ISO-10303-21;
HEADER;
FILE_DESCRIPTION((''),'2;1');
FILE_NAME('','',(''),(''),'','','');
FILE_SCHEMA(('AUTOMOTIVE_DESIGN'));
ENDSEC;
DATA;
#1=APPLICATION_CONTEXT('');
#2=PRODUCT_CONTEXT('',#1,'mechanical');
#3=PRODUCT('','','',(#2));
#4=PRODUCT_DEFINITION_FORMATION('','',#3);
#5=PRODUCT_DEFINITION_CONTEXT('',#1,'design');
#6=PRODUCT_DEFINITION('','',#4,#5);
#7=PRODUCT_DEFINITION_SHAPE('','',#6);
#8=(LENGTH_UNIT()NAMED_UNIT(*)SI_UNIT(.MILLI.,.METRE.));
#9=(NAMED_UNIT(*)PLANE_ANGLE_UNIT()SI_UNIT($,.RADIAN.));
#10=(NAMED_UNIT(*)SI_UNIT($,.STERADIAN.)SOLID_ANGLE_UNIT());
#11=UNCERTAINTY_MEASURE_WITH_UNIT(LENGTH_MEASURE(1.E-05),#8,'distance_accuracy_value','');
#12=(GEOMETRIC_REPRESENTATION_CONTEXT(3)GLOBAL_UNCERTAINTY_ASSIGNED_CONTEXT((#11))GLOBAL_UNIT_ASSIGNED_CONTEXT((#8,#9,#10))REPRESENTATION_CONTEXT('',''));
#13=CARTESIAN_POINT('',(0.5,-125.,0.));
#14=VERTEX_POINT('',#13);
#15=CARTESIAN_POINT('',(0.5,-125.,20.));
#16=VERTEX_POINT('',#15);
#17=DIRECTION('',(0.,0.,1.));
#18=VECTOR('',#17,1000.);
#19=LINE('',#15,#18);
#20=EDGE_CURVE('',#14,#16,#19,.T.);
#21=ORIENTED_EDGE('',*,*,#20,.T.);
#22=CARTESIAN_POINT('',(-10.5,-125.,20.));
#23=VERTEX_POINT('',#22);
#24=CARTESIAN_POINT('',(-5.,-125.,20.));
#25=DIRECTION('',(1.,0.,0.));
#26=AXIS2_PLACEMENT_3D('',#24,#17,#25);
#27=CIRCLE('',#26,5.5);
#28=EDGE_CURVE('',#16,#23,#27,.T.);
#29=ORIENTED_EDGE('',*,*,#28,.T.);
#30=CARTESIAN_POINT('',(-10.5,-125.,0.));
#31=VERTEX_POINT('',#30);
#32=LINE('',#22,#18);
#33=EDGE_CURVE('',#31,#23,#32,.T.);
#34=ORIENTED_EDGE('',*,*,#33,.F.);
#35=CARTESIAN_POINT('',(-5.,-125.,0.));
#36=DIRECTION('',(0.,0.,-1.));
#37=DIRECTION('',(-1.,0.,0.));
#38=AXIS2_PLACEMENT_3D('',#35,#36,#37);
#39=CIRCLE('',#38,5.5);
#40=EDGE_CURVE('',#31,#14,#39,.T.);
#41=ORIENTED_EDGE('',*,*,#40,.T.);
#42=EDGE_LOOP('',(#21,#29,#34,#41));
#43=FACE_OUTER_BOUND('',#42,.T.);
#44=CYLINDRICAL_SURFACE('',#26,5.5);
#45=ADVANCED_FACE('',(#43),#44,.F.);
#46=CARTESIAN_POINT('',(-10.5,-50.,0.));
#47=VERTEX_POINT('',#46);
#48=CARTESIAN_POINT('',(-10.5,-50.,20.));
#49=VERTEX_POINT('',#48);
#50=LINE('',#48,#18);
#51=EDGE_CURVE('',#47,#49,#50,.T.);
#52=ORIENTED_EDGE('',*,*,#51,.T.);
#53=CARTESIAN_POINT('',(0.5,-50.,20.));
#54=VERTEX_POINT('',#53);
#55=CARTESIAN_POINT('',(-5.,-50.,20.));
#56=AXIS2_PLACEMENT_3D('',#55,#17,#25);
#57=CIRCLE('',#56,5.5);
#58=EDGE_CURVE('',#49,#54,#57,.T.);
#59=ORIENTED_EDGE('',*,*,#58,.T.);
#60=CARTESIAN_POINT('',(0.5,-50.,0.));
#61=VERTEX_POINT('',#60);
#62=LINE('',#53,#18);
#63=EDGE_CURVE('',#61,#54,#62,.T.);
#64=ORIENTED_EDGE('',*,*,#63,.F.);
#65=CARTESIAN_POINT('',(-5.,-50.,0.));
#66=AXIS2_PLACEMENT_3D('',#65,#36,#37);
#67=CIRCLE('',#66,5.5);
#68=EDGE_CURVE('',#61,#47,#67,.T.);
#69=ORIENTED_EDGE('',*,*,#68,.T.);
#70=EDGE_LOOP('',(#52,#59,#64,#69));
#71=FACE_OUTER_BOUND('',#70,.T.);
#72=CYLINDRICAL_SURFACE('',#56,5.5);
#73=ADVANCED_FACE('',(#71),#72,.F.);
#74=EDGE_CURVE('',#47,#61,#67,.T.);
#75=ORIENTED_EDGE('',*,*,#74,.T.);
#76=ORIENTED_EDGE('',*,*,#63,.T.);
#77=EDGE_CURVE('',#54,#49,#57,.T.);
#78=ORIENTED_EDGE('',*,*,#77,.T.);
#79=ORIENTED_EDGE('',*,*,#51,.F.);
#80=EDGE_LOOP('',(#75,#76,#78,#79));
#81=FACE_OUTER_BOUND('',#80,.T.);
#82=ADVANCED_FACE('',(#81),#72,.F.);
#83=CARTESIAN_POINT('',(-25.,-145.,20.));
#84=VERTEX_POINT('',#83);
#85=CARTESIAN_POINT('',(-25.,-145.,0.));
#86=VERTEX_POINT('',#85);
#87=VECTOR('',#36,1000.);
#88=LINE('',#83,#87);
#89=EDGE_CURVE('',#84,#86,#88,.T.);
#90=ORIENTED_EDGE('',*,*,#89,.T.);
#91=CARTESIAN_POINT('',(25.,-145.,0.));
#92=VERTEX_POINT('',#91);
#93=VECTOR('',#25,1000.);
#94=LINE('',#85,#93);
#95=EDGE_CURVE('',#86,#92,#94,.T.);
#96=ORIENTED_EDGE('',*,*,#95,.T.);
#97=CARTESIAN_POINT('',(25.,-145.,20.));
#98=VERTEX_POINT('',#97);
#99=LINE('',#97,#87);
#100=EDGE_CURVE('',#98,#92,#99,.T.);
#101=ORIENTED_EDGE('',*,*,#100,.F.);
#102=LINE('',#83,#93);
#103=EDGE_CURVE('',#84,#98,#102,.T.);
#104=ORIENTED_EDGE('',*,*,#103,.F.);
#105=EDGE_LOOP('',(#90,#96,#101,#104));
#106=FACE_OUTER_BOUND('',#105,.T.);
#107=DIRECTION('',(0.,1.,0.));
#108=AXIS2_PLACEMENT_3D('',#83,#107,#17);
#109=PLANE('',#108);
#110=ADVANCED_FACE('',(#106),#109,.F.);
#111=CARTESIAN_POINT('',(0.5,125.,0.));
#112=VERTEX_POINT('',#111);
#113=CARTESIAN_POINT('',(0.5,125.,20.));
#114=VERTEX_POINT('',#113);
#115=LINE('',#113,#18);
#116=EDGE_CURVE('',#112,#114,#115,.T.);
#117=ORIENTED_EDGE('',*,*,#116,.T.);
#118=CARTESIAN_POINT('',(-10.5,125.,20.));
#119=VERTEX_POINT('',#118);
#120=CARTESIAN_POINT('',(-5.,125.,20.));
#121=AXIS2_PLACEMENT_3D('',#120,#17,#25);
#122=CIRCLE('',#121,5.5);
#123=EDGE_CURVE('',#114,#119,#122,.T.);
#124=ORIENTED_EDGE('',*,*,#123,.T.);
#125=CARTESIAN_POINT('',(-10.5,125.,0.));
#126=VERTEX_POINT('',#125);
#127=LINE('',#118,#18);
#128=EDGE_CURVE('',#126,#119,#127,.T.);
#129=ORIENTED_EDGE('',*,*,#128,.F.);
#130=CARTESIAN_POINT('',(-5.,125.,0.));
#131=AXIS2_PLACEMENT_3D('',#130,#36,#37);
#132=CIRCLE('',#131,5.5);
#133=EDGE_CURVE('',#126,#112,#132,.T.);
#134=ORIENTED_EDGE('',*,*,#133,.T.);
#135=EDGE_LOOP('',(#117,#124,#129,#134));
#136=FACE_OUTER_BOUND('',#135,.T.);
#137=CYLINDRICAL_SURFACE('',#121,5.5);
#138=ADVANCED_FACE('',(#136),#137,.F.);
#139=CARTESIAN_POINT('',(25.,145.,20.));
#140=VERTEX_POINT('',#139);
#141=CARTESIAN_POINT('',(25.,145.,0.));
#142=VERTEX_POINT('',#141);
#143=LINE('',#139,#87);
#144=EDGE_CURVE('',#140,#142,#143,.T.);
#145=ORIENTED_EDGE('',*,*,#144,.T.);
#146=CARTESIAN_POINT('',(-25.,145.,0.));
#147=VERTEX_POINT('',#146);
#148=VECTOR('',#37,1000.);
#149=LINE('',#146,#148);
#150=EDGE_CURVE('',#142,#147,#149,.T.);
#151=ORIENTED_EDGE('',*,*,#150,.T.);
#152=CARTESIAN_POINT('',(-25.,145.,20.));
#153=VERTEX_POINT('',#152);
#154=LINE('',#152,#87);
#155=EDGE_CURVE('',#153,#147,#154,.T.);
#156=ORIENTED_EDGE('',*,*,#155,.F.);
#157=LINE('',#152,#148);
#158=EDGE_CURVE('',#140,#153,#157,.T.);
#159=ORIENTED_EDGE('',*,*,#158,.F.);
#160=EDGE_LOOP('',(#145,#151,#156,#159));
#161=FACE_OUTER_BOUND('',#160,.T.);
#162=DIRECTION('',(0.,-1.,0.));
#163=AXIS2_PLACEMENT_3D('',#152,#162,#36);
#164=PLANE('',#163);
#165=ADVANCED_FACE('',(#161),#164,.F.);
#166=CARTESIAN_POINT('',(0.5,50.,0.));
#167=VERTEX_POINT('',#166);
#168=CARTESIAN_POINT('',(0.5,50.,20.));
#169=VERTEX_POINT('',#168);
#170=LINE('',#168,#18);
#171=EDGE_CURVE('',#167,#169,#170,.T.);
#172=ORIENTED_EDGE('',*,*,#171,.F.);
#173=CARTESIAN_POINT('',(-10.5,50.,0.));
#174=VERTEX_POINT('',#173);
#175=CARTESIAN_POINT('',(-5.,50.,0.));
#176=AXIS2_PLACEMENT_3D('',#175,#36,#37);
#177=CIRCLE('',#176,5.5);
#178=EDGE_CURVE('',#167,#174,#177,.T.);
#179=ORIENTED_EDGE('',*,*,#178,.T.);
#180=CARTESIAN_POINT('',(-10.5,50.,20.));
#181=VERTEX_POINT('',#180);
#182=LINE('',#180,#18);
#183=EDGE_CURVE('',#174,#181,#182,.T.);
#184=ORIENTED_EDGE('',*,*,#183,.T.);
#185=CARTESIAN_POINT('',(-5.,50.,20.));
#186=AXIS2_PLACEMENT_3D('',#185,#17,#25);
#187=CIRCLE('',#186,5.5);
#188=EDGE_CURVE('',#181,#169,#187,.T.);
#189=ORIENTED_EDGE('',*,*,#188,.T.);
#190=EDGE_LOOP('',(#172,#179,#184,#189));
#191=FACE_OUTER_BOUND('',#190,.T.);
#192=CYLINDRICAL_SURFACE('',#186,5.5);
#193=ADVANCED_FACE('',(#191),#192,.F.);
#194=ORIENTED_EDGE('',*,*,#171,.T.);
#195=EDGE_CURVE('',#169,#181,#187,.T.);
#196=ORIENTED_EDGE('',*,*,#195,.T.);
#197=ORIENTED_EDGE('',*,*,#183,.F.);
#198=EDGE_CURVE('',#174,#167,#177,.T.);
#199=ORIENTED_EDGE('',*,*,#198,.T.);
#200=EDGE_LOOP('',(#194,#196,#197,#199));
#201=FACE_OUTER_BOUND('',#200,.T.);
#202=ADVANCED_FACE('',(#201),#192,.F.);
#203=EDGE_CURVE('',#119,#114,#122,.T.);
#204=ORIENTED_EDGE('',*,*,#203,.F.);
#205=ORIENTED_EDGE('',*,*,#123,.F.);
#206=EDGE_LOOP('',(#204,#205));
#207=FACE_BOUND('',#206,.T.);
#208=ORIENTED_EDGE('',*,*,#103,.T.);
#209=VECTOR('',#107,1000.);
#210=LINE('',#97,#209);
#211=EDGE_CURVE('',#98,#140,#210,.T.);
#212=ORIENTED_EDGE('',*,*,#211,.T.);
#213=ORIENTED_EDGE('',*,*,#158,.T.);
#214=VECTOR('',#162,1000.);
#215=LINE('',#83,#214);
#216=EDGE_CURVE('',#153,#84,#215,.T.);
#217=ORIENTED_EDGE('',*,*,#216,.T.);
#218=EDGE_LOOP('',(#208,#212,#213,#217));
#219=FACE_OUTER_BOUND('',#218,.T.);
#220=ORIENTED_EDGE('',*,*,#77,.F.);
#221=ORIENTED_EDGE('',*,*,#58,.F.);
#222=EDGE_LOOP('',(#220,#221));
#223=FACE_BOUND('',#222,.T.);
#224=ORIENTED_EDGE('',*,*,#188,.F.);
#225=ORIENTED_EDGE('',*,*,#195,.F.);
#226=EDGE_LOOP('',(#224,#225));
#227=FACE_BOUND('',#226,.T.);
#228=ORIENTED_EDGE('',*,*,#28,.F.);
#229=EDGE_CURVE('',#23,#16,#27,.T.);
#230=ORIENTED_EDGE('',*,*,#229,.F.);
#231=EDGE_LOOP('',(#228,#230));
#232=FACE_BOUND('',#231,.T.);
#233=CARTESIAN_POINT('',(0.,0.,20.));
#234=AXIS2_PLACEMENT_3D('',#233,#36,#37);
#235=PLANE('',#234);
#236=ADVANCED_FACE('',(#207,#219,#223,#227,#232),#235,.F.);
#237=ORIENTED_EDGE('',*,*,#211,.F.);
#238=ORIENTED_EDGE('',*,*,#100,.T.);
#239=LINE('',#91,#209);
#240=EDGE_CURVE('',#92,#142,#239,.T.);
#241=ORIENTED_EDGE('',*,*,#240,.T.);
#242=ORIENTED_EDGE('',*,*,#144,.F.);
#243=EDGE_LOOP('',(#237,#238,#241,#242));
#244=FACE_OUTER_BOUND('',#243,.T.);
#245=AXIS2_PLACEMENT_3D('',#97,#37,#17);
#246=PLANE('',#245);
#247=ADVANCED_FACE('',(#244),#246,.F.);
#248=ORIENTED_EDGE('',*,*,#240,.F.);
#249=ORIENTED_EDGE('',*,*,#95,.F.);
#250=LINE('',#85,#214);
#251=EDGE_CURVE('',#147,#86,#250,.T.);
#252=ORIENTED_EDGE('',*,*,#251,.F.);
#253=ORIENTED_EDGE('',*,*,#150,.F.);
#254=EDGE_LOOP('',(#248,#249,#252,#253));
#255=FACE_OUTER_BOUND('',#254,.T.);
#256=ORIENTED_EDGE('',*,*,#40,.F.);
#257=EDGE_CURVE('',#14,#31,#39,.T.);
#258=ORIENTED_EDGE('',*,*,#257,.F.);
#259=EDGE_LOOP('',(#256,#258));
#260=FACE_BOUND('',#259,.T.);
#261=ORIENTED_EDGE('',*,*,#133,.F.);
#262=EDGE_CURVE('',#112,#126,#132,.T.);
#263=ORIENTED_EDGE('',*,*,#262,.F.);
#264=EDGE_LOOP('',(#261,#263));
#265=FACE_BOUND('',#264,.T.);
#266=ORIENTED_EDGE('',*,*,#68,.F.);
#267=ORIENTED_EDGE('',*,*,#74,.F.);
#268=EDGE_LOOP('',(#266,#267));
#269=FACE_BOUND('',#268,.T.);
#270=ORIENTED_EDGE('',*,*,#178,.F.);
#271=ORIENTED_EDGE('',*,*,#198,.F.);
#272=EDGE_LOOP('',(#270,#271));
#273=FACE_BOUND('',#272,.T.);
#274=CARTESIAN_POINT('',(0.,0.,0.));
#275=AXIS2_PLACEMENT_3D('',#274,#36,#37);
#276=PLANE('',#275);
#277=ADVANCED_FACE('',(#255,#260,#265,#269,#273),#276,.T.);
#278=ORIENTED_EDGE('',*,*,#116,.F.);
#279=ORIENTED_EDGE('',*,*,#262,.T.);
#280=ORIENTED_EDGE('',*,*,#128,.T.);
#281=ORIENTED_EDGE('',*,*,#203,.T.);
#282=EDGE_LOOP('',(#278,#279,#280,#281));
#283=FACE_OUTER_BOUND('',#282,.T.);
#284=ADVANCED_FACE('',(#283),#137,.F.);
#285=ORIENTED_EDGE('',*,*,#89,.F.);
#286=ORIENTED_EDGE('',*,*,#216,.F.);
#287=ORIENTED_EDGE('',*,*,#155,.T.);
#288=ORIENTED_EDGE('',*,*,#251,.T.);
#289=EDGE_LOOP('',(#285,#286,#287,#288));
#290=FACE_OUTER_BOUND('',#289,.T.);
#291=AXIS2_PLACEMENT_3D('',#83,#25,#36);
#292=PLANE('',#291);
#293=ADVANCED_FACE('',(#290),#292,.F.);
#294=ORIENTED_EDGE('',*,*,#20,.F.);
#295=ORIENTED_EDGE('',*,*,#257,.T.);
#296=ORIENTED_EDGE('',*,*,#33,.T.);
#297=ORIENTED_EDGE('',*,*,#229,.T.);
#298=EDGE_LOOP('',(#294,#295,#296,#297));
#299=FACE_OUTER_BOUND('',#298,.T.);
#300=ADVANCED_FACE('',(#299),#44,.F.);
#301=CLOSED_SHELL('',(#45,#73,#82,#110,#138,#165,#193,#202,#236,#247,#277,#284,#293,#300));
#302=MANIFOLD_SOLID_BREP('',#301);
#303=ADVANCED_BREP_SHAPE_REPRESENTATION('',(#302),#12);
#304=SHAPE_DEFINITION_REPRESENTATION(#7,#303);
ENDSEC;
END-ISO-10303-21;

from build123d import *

# Parameters (mm, degrees)
SKETCH_1_W                  = 50
SKETCH_1_H                  = 290
EXTRUDE_1_DEPTH             = 20
HOLE_WIZARD_11_0_11_1_D     = 11
HOLE_WIZARD_11_0_11_1_DEPTH = 36
HOLE_WIZARD_11_0_11_1_TIP   = 3.304733405


with BuildPart() as part:
    # 草图1 → 凸台-拉伸1 (new body)
    with BuildSketch(Plane.XY):
        Rectangle(SKETCH_1_W, SKETCH_1_H)
    extrude(amount=EXTRUDE_1_DEPTH)

    # Ø11.0 (11) 直径孔1
    with Locations(Plane.XY.offset(20)):
        with Locations((-5, 125), (-5, 50), (-5, -50), (-5, -125)):
            Hole(HOLE_WIZARD_11_0_11_1_D / 2, depth=HOLE_WIZARD_11_0_11_1_DEPTH)
            with Locations((0, 0, -(HOLE_WIZARD_11_0_11_1_DEPTH + HOLE_WIZARD_11_0_11_1_TIP / 2))):  # 118° drill point
                Cone(0, HOLE_WIZARD_11_0_11_1_D / 2, HOLE_WIZARD_11_0_11_1_TIP, mode=Mode.SUBTRACT)


solid = part.part
